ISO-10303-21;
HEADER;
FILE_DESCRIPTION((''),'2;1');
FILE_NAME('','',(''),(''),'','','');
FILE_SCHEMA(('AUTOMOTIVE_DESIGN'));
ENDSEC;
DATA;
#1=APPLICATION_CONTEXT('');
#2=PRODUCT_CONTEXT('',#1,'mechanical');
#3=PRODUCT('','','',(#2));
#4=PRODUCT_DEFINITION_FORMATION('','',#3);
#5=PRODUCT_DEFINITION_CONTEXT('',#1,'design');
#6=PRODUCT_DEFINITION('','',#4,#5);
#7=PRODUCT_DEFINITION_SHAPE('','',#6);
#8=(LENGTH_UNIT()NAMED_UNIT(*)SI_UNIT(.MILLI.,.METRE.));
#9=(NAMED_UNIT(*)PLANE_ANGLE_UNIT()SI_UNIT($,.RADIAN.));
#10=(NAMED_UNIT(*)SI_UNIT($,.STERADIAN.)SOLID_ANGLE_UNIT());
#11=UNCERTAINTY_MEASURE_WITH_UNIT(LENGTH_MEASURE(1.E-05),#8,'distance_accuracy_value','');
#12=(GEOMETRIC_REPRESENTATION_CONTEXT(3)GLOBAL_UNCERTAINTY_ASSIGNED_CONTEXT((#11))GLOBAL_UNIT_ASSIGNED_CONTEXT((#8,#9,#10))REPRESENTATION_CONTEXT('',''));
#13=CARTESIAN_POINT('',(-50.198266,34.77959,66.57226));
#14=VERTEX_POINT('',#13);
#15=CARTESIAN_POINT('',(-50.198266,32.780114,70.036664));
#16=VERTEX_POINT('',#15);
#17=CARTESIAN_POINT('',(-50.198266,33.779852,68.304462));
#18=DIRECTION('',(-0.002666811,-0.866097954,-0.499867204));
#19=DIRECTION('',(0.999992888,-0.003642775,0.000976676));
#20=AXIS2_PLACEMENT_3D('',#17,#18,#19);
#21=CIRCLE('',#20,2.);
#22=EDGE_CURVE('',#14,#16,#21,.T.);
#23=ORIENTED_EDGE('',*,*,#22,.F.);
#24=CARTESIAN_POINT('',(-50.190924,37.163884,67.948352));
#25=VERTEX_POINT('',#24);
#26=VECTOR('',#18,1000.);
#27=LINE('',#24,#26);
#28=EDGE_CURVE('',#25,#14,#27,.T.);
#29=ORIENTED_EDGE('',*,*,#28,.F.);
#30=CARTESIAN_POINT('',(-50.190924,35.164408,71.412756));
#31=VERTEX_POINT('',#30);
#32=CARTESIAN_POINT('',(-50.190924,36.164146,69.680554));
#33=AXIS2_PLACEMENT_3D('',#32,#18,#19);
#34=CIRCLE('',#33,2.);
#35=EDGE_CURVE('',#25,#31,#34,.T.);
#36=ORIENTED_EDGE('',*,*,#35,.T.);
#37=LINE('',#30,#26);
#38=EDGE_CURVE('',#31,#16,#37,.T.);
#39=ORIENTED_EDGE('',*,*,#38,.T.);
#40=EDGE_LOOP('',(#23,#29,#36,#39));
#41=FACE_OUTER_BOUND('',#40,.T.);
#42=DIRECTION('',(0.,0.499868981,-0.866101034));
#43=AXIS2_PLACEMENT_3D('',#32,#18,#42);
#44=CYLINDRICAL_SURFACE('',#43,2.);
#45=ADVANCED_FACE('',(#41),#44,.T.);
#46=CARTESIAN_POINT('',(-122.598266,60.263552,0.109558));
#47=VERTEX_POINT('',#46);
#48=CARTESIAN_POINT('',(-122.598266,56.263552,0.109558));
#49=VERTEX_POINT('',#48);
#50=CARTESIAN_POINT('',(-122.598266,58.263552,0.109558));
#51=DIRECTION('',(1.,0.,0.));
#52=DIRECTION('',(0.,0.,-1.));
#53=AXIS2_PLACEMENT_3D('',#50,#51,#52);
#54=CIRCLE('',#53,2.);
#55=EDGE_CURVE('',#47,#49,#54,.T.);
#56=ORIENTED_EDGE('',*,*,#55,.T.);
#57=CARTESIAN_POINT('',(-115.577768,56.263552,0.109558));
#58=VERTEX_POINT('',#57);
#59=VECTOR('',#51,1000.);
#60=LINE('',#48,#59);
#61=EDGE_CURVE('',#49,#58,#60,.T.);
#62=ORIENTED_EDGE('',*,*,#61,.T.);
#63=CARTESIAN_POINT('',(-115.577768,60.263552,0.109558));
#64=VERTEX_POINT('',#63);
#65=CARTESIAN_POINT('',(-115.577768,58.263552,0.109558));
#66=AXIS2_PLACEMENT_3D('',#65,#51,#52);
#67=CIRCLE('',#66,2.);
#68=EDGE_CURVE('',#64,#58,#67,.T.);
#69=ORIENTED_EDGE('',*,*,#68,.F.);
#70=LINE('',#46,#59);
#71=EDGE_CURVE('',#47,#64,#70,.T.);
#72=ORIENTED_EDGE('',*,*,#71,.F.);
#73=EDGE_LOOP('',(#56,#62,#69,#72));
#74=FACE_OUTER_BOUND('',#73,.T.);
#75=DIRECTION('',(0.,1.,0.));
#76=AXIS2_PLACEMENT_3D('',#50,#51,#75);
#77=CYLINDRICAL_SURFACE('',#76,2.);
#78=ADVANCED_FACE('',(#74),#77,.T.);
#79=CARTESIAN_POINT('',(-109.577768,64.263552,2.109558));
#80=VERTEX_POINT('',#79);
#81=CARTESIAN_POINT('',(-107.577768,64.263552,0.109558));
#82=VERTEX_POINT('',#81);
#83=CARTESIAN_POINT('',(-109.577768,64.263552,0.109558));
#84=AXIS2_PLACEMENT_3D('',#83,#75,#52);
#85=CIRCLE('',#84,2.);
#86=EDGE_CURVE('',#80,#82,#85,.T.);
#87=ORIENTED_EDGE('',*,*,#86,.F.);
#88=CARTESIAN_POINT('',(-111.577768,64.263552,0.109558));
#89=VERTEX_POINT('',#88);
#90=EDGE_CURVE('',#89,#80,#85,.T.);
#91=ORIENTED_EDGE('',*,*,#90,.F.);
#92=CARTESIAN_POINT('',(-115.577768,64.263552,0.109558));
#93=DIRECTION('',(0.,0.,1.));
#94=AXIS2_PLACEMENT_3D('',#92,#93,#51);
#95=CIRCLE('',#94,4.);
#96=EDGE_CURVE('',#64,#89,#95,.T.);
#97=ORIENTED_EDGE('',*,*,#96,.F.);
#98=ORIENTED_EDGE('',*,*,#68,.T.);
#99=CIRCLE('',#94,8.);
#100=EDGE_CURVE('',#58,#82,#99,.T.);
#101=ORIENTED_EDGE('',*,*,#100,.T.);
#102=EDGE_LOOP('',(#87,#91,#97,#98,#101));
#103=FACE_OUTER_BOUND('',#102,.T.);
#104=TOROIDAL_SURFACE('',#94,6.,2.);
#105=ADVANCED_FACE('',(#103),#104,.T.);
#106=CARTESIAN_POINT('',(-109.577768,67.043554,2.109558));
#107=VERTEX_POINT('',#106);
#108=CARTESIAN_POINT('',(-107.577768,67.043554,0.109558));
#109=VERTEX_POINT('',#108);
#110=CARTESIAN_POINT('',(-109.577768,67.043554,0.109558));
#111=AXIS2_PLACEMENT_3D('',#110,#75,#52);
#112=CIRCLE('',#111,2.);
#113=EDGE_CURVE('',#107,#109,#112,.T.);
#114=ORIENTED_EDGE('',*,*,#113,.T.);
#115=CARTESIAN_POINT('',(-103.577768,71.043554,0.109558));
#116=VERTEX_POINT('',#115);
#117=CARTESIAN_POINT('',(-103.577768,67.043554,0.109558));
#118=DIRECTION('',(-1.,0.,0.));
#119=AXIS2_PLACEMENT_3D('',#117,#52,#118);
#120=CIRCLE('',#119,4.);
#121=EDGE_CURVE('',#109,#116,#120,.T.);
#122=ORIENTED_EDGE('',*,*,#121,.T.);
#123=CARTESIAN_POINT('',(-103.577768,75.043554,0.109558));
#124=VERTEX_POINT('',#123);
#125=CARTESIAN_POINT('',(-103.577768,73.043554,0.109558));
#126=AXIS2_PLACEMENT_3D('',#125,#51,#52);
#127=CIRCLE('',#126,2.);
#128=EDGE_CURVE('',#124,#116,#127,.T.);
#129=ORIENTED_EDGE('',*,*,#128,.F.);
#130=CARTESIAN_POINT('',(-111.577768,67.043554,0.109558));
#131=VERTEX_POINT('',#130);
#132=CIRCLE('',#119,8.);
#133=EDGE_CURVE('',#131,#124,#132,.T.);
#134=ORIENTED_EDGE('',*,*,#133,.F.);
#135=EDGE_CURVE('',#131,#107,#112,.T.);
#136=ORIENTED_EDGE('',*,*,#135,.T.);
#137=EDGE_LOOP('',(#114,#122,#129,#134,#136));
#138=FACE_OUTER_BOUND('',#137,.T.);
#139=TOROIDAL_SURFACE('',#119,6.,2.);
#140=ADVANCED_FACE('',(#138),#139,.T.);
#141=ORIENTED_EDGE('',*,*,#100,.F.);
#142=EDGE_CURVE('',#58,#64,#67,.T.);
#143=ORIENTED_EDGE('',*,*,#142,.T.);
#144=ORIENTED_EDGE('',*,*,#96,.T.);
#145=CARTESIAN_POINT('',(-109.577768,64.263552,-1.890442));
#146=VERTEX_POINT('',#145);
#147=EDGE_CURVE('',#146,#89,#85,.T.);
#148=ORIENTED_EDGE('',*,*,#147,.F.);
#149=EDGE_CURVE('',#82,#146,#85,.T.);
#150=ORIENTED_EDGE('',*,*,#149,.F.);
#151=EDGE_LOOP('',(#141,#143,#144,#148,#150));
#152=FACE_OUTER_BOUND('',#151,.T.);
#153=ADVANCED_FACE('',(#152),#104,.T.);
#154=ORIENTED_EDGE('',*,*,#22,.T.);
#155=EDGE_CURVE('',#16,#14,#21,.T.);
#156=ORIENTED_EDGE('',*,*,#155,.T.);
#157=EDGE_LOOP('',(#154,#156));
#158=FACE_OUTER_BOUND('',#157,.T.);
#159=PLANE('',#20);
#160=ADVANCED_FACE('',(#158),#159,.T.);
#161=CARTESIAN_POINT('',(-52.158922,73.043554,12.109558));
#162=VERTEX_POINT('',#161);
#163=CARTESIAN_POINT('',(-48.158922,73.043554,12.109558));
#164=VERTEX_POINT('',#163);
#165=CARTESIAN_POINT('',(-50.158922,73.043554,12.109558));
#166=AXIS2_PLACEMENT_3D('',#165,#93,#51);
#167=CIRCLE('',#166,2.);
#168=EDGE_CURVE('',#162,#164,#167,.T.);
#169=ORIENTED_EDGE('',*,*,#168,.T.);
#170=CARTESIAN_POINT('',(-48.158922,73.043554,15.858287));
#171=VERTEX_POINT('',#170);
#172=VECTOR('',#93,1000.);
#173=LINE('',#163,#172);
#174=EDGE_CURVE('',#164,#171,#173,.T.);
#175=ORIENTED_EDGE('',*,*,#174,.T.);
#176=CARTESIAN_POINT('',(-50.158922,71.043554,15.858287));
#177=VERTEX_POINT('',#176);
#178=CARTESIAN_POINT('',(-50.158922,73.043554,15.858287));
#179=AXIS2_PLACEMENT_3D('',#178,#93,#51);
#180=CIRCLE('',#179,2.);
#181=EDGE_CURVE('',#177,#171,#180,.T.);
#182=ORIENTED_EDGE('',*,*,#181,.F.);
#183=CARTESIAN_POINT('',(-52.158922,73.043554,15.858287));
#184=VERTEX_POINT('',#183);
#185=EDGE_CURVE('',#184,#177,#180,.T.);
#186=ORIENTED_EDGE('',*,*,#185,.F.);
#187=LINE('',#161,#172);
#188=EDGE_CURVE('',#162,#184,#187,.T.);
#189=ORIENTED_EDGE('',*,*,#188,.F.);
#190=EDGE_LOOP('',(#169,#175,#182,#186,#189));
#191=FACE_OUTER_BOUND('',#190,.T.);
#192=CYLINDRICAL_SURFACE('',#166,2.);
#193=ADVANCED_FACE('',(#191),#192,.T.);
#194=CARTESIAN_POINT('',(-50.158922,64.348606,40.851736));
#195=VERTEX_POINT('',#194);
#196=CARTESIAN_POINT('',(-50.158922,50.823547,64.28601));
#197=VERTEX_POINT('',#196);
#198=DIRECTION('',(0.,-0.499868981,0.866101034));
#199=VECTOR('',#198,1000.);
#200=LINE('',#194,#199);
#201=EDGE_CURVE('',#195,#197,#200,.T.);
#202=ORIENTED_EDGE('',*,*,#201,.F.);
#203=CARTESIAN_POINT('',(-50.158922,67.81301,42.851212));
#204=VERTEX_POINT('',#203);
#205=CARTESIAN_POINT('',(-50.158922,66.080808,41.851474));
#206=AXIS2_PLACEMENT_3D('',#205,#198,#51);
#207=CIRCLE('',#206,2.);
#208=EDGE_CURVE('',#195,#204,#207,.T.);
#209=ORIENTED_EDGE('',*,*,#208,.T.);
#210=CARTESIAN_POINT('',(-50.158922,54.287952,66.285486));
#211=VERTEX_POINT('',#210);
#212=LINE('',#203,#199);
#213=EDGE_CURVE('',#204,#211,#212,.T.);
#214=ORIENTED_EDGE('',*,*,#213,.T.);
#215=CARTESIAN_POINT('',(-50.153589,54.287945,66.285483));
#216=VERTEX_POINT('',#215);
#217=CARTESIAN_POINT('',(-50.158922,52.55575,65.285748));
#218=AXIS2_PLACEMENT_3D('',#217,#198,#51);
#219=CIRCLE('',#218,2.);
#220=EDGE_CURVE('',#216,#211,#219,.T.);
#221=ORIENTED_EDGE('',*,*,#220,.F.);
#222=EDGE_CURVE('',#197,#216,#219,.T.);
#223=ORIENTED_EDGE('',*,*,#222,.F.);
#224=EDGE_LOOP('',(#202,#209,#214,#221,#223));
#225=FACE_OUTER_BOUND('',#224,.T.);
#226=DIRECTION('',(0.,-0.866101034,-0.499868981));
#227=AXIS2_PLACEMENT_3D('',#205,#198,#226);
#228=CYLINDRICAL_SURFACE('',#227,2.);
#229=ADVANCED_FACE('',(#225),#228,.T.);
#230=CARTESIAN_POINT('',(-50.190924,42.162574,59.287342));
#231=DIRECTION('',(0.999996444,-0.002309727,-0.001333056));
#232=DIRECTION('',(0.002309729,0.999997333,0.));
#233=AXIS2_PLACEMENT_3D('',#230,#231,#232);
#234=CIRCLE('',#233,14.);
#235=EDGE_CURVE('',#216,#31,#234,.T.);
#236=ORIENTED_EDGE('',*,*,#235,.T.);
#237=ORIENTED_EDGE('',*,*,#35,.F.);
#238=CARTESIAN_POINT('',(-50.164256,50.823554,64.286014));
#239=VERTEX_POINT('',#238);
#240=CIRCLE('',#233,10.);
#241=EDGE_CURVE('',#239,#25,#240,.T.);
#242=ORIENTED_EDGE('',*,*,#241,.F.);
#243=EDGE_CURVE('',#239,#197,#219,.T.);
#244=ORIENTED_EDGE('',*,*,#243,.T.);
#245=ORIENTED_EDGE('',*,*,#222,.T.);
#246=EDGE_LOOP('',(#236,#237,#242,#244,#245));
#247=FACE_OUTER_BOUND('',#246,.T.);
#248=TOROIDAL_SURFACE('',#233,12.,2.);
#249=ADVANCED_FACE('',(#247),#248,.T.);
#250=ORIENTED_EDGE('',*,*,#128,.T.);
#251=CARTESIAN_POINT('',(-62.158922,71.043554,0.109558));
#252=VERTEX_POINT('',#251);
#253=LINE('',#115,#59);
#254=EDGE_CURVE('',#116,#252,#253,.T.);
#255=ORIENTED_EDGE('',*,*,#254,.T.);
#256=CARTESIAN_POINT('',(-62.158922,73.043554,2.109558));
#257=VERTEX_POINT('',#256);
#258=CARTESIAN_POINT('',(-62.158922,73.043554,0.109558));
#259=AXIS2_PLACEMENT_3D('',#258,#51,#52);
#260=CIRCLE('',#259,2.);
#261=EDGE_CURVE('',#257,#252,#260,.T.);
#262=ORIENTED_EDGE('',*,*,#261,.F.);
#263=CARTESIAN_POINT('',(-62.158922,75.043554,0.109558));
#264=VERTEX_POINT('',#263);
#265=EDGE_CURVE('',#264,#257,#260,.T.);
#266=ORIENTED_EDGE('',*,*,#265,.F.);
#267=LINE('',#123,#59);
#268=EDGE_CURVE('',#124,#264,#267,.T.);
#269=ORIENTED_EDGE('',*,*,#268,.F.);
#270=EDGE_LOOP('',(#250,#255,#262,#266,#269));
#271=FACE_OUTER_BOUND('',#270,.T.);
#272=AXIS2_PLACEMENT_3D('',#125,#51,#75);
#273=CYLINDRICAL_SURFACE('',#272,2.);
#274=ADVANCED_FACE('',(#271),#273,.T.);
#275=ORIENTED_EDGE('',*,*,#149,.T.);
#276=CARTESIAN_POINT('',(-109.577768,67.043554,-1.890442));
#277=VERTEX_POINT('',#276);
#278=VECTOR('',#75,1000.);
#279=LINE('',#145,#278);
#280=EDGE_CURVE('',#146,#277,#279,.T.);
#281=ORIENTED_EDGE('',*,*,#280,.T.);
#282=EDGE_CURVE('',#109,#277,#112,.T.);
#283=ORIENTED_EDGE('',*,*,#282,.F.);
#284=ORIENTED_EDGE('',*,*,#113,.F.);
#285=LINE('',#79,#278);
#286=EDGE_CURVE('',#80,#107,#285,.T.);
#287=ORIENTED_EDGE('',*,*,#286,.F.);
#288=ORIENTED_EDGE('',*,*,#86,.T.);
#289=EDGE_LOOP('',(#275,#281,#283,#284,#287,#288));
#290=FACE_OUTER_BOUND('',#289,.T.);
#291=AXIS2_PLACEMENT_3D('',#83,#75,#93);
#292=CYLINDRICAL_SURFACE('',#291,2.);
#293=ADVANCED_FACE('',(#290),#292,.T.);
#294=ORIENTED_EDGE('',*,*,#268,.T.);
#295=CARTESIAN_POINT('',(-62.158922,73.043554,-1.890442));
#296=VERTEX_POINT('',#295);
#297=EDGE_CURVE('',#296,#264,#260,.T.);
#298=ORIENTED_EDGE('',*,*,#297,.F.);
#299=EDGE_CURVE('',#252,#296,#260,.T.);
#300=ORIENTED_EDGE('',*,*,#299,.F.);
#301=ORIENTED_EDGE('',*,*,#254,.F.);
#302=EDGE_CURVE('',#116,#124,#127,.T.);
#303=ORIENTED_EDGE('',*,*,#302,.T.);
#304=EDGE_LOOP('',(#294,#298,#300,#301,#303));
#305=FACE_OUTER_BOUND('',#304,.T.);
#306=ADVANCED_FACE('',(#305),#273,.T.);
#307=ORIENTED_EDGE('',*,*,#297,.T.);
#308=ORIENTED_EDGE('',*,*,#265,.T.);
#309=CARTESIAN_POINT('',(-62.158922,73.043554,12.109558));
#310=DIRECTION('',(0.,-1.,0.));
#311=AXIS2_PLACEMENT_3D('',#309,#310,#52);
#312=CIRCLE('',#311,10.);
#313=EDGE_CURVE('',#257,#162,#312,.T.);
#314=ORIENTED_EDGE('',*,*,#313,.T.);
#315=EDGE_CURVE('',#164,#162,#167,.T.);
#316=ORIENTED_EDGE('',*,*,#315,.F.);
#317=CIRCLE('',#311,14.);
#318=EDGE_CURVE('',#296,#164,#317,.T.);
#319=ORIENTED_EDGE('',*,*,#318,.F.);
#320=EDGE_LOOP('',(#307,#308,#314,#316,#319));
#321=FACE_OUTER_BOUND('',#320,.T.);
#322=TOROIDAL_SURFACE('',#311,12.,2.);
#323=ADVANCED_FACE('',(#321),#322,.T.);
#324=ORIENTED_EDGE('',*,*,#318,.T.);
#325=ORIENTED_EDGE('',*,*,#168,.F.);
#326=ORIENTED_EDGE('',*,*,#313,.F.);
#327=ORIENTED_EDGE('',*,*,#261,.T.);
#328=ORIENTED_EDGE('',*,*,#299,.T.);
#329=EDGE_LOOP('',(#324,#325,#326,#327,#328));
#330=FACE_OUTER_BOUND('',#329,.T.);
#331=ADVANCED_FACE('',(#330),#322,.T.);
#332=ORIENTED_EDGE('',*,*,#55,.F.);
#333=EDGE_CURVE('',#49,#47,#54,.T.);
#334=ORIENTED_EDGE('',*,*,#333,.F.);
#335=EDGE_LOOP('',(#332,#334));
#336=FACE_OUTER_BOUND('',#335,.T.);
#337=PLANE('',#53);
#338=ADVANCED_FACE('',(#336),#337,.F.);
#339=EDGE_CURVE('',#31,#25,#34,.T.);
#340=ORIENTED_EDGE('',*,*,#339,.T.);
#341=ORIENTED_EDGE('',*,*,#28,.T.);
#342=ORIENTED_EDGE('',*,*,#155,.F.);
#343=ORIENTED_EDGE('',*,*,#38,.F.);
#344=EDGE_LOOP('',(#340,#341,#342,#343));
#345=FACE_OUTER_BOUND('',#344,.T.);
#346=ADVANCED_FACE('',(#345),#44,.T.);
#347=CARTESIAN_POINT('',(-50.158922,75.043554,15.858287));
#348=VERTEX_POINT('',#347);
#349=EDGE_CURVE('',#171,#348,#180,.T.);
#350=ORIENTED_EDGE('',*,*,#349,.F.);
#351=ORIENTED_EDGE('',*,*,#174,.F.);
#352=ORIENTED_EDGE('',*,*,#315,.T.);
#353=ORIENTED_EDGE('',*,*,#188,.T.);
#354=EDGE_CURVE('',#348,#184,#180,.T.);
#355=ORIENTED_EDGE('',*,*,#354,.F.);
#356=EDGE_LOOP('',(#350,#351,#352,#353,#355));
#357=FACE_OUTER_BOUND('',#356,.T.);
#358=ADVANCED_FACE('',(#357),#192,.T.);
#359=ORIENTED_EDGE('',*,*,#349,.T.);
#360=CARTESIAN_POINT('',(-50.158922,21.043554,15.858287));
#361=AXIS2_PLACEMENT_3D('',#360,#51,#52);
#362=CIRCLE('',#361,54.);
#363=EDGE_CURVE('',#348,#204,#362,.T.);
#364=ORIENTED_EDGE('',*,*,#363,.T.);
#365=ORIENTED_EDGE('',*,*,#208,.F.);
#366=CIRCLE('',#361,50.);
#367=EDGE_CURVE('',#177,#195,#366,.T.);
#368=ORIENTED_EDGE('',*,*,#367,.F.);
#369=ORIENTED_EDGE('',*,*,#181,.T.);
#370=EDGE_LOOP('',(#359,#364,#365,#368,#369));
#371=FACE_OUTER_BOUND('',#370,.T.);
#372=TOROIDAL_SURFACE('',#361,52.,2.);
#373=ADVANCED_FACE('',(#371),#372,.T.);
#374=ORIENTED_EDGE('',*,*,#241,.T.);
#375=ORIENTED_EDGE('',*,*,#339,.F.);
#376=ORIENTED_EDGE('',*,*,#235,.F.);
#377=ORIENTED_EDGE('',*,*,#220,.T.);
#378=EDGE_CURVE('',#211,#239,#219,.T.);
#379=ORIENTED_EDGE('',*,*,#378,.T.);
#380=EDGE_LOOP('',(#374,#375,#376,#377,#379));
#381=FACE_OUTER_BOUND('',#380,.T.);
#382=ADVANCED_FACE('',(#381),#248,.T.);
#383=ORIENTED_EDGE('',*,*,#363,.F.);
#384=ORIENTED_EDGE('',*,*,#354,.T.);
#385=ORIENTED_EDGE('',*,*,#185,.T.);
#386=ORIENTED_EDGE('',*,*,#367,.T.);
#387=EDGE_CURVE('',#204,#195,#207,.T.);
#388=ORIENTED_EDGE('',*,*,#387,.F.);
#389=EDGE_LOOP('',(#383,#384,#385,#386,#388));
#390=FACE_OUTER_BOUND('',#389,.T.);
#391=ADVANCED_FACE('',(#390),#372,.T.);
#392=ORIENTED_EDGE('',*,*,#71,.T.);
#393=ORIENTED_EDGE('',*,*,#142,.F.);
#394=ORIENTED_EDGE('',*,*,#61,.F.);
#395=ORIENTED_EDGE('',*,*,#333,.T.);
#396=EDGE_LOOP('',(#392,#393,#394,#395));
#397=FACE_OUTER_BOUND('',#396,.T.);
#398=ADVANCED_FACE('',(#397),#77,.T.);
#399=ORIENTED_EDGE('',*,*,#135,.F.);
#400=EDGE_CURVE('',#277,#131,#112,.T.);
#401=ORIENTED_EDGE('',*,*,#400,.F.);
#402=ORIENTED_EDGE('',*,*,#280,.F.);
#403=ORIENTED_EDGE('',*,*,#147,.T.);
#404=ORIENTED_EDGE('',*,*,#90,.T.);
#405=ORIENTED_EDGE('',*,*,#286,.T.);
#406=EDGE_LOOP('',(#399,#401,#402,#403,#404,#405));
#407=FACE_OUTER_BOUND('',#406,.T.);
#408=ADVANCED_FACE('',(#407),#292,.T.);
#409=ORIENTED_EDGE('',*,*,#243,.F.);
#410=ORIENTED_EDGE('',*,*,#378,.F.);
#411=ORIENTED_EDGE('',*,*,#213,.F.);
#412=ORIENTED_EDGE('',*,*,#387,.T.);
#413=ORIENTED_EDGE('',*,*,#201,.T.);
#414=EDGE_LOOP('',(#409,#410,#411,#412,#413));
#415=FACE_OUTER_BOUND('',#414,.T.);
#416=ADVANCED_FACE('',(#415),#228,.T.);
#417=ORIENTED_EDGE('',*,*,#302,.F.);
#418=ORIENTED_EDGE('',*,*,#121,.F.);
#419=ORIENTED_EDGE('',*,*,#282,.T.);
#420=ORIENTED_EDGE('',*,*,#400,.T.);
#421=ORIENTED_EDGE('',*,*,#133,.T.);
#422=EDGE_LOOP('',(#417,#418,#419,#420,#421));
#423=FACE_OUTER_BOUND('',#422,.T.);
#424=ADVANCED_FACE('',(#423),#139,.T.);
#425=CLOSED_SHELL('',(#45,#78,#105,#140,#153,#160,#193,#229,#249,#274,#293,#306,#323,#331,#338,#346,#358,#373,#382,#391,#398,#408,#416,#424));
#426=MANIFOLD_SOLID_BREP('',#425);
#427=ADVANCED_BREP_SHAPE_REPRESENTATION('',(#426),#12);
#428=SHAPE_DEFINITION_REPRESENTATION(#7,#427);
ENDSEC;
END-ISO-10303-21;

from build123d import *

# Parameters (mm, degrees)
SKETCH1_R = 2


with BuildPart() as part:
    # Sweep1: sweep along a curve in space
    with BuildLine() as sweep1_path:
        Line((-50.19826571, 33.779851644, 68.304462045), (-50.190924205, 36.164146317, 69.680554329))
        ThreePointArc((-50.190924205, 36.164146317, 69.680554329), (-50.168295566, 45.270129978, 70.877966766), (-50.158922477, 52.555749547, 65.285748364))
        Line((-50.158922477, 52.555749547, 65.285748364), (-50.158922477, 66.080807741, 41.85147393))
        ThreePointArc((-50.158922477, 73.043553961, 15.8582869), (-50.158922477, 71.272714796, 29.313077932), (-50.158922477, 66.080807741, 41.85147393))
        Line((-50.158922477, 73.043553961, 15.8582869), (-50.158922477, 73.043553961, 12.109558404))
        ThreePointArc((-62.158922477, 73.043553961, 0.109558404), (-53.673641103, 73.043553961, 3.62427703), (-50.158922477, 73.043553961, 12.109558404))
        Line((-103.577768148, 73.043553961, 0.109558404), (-62.158922477, 73.043553961, 0.109558404))
        ThreePointArc((-103.577768148, 73.043553961, 0.109558404), (-107.820408835, 71.286194648, 0.109558404), (-109.577768148, 67.043553961, 0.109558404))
        Line((-109.577768148, 64.263552475, 0.109558404), (-109.577768148, 67.043553961, 0.109558404))
        ThreePointArc((-109.577768148, 64.263552475, 0.109558404), (-111.335127461, 60.020911788, 0.109558404), (-115.577768148, 58.263552475, 0.109558404))
        Line((-122.59826571, 58.263552475, 0.109558404), (-115.577768148, 58.263552475, 0.109558404))
    # Sketch1 → Sweep1 (sweep)
    with BuildSketch(Plane(origin=(-122.59826571, 0, 0), x_dir=(0, 0, -1), z_dir=(1, 0, 0))):
        with Locations((-0.109558404, 58.263552475)):
            Circle(SKETCH1_R)
    sweep(path=sweep1_path.line)


solid = part.part
